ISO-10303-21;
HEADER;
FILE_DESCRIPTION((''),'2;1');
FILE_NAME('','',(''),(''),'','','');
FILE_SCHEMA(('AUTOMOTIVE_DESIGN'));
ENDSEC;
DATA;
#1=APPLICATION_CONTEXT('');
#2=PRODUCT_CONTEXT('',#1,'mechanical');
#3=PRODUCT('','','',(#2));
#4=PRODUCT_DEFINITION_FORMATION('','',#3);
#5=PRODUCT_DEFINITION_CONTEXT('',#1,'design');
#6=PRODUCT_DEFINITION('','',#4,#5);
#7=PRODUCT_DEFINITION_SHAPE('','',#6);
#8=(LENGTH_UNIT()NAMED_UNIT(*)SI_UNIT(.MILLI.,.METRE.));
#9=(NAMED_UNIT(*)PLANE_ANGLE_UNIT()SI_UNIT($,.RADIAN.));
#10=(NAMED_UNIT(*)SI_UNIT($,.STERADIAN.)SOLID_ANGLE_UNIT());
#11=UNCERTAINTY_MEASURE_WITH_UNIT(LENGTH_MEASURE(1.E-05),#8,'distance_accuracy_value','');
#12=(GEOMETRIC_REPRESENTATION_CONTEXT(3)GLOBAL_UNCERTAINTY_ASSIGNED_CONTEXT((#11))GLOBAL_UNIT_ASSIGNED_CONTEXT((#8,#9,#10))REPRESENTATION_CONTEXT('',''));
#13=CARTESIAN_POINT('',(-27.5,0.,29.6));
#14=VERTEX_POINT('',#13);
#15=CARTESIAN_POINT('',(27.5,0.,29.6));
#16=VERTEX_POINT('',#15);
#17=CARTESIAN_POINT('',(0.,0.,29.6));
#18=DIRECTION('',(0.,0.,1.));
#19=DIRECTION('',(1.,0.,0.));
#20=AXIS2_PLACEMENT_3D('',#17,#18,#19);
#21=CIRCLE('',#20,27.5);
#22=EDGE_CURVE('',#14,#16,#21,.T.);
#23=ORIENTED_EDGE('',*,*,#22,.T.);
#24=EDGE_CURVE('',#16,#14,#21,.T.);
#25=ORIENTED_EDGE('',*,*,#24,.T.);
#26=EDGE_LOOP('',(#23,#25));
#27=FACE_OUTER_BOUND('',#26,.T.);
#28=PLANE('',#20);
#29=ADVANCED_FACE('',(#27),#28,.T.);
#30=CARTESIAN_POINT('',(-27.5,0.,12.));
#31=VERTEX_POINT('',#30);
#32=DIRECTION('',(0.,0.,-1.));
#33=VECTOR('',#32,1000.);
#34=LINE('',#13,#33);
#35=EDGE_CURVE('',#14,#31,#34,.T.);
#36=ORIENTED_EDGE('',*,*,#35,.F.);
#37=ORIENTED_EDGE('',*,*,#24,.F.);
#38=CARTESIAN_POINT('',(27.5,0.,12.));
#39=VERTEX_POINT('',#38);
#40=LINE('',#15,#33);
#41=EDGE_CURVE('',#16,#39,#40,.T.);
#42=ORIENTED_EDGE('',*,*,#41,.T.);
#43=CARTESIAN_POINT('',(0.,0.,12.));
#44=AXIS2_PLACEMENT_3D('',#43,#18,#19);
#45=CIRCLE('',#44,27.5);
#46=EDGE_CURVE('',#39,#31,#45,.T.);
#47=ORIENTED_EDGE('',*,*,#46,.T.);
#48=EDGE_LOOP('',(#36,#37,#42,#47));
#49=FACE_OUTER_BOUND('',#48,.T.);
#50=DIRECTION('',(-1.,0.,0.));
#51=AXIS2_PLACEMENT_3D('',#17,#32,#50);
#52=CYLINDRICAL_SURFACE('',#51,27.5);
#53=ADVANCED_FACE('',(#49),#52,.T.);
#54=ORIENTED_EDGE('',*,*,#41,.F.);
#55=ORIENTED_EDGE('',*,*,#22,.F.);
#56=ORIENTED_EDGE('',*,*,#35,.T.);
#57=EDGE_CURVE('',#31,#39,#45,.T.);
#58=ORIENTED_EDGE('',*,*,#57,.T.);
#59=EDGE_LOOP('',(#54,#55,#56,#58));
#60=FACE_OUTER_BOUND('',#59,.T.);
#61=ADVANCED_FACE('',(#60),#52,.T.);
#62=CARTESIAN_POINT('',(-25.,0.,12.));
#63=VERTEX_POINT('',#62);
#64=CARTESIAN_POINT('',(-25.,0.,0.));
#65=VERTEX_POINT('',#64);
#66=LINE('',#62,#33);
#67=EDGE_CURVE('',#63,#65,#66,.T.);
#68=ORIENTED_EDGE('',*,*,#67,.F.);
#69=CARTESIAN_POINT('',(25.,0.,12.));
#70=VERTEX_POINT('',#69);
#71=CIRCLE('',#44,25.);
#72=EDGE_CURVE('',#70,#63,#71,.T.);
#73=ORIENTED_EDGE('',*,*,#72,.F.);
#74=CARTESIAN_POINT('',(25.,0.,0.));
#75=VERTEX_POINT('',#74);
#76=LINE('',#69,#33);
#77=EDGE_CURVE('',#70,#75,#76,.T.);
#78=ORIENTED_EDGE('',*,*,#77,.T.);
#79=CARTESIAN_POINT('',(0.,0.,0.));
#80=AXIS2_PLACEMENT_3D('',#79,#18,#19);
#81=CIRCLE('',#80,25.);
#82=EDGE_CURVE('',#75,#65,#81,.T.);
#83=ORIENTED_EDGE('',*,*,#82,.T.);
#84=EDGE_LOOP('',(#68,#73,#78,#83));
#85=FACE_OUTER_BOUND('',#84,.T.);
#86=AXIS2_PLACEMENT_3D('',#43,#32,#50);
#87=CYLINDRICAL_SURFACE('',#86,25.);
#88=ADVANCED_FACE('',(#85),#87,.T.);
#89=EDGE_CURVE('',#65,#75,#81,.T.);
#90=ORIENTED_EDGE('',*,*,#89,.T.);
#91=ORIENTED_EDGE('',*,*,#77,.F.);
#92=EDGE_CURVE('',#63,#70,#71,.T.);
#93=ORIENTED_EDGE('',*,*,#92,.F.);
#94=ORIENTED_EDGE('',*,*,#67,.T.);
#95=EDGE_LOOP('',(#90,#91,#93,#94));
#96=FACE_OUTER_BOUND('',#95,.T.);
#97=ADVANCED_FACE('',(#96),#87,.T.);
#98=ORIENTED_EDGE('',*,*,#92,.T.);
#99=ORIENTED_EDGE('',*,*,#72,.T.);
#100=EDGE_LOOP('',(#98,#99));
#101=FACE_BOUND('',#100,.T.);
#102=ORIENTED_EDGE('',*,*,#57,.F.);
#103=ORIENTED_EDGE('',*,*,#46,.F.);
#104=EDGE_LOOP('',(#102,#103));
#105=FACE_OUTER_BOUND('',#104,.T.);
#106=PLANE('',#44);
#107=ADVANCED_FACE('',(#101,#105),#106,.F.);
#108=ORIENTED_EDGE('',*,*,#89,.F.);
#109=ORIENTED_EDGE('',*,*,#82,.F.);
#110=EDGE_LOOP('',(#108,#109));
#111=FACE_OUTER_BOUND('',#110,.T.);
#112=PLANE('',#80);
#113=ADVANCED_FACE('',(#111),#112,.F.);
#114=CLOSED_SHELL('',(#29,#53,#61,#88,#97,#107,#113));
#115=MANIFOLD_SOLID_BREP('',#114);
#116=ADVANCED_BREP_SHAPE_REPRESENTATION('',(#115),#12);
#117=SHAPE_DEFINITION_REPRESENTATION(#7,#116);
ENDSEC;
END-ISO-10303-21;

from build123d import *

# Parameters (mm, degrees)
SKETCH1_R           = 25
BOSS_EXTRUDE1_DEPTH = 12
SKETCH2_R           = 27.5
BOSS_EXTRUDE2_DEPTH = 17.6


with BuildPart() as part:
    # Sketch1 → Boss-Extrude1 (new body)
    with BuildSketch(Plane.XY):
        Circle(SKETCH1_R)
    extrude(amount=BOSS_EXTRUDE1_DEPTH)

    # Sketch2 → Boss-Extrude2 (add)
    with BuildSketch(Plane.XY.offset(12)):
        Circle(SKETCH2_R)
    extrude(amount=BOSS_EXTRUDE2_DEPTH)


solid = part.part
